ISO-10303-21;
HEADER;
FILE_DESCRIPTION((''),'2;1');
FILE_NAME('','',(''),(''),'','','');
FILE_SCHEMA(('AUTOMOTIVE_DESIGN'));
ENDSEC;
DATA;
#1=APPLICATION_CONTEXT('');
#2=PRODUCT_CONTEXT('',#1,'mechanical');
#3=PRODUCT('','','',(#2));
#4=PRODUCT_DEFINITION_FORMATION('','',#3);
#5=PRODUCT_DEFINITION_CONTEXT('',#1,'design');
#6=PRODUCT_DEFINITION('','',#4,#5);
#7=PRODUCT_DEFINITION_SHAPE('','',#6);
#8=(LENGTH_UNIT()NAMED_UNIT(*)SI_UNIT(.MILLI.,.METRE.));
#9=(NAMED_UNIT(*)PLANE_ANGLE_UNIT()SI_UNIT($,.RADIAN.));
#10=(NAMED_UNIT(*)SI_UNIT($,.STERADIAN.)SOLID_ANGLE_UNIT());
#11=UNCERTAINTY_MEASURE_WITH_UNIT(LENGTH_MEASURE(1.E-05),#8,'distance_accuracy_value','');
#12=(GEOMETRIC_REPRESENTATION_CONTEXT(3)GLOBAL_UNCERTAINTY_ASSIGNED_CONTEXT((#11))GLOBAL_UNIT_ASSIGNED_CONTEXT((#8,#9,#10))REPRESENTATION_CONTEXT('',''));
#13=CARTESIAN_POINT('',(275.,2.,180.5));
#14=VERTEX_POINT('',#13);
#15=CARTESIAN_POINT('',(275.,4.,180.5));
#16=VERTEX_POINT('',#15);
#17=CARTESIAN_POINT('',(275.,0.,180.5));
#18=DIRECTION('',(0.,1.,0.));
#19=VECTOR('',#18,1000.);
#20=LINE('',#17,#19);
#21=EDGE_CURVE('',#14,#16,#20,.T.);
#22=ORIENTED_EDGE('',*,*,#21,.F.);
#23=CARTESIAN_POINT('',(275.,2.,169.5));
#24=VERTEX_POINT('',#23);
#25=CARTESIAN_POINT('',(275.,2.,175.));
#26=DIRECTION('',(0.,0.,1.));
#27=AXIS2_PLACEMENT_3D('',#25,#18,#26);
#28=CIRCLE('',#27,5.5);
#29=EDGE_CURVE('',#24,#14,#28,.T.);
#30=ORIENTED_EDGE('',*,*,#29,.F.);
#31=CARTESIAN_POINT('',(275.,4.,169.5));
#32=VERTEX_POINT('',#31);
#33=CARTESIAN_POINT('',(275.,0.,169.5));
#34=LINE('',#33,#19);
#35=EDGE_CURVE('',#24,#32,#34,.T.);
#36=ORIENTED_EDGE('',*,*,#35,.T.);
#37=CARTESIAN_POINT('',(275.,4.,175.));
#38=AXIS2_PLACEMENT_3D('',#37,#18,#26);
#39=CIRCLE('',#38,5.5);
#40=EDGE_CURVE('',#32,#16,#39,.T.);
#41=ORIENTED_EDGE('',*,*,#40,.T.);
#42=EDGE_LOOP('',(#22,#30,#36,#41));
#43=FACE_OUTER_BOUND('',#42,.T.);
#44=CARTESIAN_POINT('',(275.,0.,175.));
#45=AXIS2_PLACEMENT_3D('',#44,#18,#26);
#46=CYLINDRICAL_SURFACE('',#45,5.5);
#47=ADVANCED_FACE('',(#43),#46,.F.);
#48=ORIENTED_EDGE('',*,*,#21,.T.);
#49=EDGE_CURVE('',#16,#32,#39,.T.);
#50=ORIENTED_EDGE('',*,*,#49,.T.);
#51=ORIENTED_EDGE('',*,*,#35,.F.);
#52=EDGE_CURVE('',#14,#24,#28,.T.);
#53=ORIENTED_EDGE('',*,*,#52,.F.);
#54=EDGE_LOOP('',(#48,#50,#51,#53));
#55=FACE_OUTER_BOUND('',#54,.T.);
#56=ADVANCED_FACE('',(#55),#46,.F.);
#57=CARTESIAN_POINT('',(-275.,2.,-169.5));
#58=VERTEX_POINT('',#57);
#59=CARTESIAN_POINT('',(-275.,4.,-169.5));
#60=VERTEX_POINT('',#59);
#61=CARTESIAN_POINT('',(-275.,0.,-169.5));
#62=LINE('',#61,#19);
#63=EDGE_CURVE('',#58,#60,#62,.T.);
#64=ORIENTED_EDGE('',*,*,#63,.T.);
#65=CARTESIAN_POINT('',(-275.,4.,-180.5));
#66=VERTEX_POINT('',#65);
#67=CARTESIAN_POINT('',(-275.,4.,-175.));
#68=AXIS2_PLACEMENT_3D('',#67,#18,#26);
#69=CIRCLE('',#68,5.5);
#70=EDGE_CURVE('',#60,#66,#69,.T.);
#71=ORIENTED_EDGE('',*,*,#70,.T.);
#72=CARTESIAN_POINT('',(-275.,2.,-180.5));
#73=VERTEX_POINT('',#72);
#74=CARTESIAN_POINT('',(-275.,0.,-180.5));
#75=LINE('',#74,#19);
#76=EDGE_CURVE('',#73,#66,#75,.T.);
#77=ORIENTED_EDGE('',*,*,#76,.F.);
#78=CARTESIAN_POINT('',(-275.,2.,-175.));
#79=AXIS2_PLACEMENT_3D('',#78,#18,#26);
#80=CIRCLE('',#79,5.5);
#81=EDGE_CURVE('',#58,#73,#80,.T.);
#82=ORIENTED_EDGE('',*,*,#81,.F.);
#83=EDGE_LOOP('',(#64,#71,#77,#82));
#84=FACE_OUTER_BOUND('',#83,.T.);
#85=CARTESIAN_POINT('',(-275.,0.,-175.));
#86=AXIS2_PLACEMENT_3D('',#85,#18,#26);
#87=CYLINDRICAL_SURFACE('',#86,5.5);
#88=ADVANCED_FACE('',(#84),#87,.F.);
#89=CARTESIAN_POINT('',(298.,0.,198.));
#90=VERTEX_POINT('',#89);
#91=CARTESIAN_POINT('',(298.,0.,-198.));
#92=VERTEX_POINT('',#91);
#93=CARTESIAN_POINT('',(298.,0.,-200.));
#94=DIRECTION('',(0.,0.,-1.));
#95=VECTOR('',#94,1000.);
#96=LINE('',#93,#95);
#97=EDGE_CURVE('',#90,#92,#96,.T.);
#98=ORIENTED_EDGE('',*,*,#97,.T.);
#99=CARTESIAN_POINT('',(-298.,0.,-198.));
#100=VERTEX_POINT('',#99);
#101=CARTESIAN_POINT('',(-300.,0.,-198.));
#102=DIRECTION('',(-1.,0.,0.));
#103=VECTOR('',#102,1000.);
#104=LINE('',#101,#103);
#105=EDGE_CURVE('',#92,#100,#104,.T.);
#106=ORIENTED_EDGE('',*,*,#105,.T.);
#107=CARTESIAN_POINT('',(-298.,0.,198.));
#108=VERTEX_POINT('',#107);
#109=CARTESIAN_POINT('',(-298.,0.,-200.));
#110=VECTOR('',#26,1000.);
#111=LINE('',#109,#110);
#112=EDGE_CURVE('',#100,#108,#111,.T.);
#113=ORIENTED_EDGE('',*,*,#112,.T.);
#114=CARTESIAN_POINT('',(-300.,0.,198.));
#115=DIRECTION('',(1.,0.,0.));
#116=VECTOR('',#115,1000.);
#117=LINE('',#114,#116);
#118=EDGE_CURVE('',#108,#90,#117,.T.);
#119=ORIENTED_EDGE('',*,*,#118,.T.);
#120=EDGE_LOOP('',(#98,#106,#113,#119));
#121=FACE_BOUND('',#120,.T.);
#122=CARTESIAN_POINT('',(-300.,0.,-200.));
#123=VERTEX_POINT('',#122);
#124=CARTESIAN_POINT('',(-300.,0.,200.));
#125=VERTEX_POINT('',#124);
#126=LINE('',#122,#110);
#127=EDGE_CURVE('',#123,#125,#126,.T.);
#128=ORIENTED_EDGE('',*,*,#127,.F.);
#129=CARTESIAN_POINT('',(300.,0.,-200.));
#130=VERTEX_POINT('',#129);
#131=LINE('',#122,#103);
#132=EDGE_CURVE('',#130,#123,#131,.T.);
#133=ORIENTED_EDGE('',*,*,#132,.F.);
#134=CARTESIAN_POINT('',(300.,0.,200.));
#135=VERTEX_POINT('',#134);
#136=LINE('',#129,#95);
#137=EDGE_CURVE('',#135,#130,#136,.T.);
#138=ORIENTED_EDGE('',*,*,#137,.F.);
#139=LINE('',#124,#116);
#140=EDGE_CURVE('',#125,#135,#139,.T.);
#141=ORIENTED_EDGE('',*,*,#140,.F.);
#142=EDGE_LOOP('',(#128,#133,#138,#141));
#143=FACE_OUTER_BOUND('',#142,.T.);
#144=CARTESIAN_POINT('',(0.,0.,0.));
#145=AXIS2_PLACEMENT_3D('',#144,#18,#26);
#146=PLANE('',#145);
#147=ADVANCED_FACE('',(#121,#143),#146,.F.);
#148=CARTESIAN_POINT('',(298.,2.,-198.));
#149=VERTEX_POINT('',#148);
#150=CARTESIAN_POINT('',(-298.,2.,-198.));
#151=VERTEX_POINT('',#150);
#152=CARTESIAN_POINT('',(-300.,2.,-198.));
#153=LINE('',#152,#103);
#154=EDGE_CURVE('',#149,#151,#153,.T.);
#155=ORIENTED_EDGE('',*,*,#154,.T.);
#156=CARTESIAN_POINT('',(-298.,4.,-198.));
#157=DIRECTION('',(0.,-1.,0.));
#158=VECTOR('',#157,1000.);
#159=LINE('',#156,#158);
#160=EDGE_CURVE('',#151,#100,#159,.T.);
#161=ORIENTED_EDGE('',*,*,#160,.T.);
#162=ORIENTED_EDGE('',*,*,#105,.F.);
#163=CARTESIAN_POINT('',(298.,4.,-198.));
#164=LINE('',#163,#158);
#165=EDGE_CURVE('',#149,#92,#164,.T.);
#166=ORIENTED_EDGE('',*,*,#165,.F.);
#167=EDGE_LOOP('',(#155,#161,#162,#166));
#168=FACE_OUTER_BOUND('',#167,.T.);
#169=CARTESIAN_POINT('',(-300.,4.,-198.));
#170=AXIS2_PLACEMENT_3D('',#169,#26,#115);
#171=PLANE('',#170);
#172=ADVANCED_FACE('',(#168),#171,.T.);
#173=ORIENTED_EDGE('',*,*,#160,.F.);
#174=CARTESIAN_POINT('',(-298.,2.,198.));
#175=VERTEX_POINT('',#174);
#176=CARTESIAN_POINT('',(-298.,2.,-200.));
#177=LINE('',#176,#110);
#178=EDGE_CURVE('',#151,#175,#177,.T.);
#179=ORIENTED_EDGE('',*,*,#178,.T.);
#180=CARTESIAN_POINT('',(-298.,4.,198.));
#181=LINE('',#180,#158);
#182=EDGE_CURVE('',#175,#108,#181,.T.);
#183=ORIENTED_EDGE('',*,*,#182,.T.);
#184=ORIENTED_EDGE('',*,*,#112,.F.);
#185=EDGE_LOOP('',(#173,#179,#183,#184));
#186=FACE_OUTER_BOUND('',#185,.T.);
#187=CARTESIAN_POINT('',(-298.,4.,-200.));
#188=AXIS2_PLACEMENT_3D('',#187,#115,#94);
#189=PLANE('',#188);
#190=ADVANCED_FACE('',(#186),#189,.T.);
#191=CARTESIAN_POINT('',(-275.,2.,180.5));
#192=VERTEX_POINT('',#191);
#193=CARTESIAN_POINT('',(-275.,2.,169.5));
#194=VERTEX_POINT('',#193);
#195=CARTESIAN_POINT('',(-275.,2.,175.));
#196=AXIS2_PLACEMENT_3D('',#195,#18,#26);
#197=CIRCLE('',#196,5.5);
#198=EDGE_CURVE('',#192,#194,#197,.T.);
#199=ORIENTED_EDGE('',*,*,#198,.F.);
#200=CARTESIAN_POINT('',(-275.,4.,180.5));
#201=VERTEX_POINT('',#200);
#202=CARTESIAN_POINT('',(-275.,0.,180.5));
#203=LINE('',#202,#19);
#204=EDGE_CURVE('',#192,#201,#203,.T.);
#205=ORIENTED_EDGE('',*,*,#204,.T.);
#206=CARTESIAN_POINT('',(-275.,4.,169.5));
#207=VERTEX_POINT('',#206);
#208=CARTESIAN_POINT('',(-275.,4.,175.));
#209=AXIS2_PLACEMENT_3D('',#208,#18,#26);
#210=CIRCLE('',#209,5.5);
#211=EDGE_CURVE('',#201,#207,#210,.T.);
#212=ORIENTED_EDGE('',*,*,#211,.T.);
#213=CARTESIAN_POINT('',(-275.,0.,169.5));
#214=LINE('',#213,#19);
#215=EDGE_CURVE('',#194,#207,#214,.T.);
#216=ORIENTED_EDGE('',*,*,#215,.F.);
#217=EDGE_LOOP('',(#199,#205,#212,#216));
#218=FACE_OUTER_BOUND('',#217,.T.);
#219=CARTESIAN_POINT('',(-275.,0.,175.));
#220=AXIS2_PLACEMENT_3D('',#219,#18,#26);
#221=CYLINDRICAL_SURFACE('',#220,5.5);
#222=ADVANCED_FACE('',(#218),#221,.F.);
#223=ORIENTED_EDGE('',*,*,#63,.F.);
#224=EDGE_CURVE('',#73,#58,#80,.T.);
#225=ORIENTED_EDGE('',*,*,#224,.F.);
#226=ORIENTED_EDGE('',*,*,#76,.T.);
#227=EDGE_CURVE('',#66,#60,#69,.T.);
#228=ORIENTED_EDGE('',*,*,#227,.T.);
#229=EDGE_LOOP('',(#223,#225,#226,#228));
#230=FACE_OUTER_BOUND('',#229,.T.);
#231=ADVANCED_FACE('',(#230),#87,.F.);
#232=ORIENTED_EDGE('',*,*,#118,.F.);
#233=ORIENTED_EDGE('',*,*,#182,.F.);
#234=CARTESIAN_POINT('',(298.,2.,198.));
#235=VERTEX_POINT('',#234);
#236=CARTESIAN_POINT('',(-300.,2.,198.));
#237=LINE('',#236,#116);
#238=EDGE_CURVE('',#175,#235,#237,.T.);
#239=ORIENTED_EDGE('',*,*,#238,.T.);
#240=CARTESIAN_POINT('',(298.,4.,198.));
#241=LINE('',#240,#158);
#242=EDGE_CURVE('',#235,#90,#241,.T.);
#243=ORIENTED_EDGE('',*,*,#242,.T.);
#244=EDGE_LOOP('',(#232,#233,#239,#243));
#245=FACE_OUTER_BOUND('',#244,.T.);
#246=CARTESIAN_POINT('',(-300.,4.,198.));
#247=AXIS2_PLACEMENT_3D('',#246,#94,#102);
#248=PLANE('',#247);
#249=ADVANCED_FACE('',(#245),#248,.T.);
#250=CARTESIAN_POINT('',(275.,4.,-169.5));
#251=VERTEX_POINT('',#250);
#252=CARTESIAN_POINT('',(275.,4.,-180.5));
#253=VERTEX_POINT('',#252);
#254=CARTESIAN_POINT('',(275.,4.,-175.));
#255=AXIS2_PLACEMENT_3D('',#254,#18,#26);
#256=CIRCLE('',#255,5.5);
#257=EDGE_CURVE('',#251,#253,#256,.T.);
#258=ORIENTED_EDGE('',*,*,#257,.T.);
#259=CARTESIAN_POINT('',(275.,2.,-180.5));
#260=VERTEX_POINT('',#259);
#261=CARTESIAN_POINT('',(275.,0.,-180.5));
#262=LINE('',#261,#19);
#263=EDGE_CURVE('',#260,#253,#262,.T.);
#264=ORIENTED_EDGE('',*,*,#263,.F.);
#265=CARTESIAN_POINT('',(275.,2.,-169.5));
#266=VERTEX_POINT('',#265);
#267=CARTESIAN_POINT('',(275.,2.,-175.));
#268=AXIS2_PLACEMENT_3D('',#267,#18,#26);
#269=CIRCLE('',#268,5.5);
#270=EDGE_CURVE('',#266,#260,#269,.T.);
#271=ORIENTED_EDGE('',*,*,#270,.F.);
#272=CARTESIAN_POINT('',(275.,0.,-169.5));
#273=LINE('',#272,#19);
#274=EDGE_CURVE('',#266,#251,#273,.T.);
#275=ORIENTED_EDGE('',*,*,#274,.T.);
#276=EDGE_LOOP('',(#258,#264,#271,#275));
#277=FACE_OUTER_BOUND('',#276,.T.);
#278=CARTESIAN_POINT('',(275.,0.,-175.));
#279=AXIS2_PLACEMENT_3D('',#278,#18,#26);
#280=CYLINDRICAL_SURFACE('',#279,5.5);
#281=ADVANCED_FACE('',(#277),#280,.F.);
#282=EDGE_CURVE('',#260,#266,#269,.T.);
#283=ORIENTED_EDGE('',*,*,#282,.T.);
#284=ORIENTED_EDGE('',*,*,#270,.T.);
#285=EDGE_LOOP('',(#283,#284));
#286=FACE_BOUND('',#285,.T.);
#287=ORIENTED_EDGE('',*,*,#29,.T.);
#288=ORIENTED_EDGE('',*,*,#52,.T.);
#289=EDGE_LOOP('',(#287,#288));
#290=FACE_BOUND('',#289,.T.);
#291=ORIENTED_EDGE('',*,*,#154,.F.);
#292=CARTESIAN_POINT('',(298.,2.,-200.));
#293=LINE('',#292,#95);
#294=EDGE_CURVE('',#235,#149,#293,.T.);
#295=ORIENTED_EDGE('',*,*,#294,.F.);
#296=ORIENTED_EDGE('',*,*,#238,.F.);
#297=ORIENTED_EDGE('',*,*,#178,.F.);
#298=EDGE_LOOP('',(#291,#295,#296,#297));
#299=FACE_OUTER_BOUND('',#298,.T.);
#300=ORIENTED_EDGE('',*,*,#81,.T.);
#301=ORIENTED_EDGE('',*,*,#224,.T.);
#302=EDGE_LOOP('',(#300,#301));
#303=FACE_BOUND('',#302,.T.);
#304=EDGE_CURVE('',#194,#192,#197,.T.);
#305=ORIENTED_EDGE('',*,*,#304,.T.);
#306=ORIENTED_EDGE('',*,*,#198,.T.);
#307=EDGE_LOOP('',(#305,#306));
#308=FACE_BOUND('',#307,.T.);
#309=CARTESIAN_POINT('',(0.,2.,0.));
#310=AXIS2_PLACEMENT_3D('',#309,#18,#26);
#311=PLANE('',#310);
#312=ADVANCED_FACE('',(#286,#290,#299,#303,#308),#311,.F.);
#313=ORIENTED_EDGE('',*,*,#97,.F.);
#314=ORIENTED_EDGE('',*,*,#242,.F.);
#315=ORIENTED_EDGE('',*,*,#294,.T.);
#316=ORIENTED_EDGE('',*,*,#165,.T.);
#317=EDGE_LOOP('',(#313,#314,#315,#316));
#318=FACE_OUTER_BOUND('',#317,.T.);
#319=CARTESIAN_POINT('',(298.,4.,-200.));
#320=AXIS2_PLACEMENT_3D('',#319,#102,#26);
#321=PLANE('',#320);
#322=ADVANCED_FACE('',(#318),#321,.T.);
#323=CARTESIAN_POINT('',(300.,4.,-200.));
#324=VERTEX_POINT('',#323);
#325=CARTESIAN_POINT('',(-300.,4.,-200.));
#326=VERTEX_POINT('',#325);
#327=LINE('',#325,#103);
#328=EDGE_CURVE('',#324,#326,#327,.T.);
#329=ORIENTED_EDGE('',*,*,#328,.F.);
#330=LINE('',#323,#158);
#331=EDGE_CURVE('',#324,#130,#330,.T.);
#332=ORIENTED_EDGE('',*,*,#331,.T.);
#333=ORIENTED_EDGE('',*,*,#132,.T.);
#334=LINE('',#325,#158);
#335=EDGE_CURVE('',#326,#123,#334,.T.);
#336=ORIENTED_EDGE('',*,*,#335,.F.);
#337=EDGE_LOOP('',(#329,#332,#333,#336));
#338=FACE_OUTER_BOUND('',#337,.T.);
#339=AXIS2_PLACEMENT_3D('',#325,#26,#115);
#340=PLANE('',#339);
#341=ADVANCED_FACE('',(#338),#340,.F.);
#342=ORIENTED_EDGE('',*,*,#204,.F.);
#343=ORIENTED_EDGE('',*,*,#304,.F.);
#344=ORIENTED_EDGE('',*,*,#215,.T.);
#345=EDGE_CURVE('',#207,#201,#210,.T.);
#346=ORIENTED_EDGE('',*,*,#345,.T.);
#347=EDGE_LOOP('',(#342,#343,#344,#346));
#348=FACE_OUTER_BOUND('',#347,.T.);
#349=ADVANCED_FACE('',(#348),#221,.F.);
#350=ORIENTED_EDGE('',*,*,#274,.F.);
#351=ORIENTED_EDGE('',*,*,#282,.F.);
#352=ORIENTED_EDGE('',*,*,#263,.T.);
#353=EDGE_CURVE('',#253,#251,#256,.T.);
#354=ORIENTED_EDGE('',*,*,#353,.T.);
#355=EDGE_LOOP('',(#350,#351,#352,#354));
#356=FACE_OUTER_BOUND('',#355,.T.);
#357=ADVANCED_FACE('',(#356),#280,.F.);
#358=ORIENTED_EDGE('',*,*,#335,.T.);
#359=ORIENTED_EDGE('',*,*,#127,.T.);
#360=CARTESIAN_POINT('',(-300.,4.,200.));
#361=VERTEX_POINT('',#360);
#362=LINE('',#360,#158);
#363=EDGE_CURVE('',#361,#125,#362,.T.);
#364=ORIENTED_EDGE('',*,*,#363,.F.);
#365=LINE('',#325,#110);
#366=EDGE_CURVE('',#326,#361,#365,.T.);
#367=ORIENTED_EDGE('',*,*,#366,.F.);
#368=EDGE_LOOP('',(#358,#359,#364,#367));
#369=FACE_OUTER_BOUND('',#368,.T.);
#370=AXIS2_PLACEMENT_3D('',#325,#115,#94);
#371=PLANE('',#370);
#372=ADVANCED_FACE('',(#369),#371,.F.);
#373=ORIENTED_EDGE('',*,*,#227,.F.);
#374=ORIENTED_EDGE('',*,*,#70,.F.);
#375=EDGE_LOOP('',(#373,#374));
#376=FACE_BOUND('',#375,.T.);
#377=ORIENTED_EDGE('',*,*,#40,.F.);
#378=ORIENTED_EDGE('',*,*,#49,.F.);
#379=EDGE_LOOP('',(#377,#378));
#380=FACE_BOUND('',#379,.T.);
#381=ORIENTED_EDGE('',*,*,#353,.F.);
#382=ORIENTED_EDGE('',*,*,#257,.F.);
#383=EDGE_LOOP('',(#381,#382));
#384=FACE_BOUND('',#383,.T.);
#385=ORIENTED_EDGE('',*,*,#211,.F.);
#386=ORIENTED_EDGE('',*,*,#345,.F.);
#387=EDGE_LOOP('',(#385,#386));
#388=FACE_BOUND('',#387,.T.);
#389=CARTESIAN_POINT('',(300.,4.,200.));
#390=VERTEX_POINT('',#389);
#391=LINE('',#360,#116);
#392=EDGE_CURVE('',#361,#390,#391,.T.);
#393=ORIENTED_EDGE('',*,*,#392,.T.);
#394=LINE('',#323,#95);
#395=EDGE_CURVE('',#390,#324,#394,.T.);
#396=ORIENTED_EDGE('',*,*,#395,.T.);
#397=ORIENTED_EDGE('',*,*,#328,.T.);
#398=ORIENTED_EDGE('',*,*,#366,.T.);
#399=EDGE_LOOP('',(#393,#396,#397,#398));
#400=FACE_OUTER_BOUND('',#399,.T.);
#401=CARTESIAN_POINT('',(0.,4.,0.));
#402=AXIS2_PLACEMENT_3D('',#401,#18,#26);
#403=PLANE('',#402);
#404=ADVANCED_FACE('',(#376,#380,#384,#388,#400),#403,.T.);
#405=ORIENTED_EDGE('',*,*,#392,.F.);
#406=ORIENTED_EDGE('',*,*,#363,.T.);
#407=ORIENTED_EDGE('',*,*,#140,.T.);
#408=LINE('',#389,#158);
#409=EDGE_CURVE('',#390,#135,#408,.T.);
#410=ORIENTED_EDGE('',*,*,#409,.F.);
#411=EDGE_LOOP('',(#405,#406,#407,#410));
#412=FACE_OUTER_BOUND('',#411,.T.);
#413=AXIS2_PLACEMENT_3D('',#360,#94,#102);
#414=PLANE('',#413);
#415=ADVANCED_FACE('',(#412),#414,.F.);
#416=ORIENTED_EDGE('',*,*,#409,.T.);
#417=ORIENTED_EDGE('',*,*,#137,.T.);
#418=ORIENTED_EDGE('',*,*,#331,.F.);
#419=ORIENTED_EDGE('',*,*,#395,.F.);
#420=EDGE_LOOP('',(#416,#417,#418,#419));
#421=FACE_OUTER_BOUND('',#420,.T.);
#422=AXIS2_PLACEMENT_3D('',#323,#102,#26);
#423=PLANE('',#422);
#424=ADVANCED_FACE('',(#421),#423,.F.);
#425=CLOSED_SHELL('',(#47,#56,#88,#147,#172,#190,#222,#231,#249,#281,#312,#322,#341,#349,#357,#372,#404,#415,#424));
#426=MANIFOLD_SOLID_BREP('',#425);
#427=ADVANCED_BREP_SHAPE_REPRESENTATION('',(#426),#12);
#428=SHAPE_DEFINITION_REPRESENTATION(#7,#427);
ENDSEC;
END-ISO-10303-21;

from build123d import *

# Parameters (mm, degrees)
SKETCH1_W           = 600
SKETCH1_H           = 400
BOSS_EXTRUDE1_DEPTH = 4
SHELL1_T            = -2
SKETCH2_R           = 5.5
CUT_EXTRUDE1_DEPTH  = 4


with BuildPart() as part:
    # Sketch1 → Boss-Extrude1 (new body)
    with BuildSketch(Plane(origin=(0, 0, 0), x_dir=(1, 0, 0), z_dir=(0, 1, 0))):
        Rectangle(SKETCH1_W, SKETCH1_H)
    extrude(amount=BOSS_EXTRUDE1_DEPTH)

    # Shell1
    shell1_openings = [part.faces().sort_by_distance(p)[0] for p in [
        (0, 0, 0),
    ]]
    offset(amount=SHELL1_T, openings=shell1_openings, kind=Kind.INTERSECTION)

    # Sketch2 → Cut-Extrude1 (cut)
    with BuildSketch(Plane(origin=(0, 4, 0), x_dir=(1, 0, 0), z_dir=(0, 1, 0))):
        with Locations(Location((-275, 175, 0), (0, 0, 270))):
            Circle(SKETCH2_R)
        with Locations(Location((275, 175, 0), (0, 0, 270))):
            Circle(SKETCH2_R)
        with Locations(Location((275, -175, 0), (0, 0, 270))):
            Circle(SKETCH2_R)
        with Locations(Location((-275, -175, 0), (0, 0, 270))):
            Circle(SKETCH2_R)
    extrude(amount=-CUT_EXTRUDE1_DEPTH, mode=Mode.SUBTRACT)


solid = part.part
